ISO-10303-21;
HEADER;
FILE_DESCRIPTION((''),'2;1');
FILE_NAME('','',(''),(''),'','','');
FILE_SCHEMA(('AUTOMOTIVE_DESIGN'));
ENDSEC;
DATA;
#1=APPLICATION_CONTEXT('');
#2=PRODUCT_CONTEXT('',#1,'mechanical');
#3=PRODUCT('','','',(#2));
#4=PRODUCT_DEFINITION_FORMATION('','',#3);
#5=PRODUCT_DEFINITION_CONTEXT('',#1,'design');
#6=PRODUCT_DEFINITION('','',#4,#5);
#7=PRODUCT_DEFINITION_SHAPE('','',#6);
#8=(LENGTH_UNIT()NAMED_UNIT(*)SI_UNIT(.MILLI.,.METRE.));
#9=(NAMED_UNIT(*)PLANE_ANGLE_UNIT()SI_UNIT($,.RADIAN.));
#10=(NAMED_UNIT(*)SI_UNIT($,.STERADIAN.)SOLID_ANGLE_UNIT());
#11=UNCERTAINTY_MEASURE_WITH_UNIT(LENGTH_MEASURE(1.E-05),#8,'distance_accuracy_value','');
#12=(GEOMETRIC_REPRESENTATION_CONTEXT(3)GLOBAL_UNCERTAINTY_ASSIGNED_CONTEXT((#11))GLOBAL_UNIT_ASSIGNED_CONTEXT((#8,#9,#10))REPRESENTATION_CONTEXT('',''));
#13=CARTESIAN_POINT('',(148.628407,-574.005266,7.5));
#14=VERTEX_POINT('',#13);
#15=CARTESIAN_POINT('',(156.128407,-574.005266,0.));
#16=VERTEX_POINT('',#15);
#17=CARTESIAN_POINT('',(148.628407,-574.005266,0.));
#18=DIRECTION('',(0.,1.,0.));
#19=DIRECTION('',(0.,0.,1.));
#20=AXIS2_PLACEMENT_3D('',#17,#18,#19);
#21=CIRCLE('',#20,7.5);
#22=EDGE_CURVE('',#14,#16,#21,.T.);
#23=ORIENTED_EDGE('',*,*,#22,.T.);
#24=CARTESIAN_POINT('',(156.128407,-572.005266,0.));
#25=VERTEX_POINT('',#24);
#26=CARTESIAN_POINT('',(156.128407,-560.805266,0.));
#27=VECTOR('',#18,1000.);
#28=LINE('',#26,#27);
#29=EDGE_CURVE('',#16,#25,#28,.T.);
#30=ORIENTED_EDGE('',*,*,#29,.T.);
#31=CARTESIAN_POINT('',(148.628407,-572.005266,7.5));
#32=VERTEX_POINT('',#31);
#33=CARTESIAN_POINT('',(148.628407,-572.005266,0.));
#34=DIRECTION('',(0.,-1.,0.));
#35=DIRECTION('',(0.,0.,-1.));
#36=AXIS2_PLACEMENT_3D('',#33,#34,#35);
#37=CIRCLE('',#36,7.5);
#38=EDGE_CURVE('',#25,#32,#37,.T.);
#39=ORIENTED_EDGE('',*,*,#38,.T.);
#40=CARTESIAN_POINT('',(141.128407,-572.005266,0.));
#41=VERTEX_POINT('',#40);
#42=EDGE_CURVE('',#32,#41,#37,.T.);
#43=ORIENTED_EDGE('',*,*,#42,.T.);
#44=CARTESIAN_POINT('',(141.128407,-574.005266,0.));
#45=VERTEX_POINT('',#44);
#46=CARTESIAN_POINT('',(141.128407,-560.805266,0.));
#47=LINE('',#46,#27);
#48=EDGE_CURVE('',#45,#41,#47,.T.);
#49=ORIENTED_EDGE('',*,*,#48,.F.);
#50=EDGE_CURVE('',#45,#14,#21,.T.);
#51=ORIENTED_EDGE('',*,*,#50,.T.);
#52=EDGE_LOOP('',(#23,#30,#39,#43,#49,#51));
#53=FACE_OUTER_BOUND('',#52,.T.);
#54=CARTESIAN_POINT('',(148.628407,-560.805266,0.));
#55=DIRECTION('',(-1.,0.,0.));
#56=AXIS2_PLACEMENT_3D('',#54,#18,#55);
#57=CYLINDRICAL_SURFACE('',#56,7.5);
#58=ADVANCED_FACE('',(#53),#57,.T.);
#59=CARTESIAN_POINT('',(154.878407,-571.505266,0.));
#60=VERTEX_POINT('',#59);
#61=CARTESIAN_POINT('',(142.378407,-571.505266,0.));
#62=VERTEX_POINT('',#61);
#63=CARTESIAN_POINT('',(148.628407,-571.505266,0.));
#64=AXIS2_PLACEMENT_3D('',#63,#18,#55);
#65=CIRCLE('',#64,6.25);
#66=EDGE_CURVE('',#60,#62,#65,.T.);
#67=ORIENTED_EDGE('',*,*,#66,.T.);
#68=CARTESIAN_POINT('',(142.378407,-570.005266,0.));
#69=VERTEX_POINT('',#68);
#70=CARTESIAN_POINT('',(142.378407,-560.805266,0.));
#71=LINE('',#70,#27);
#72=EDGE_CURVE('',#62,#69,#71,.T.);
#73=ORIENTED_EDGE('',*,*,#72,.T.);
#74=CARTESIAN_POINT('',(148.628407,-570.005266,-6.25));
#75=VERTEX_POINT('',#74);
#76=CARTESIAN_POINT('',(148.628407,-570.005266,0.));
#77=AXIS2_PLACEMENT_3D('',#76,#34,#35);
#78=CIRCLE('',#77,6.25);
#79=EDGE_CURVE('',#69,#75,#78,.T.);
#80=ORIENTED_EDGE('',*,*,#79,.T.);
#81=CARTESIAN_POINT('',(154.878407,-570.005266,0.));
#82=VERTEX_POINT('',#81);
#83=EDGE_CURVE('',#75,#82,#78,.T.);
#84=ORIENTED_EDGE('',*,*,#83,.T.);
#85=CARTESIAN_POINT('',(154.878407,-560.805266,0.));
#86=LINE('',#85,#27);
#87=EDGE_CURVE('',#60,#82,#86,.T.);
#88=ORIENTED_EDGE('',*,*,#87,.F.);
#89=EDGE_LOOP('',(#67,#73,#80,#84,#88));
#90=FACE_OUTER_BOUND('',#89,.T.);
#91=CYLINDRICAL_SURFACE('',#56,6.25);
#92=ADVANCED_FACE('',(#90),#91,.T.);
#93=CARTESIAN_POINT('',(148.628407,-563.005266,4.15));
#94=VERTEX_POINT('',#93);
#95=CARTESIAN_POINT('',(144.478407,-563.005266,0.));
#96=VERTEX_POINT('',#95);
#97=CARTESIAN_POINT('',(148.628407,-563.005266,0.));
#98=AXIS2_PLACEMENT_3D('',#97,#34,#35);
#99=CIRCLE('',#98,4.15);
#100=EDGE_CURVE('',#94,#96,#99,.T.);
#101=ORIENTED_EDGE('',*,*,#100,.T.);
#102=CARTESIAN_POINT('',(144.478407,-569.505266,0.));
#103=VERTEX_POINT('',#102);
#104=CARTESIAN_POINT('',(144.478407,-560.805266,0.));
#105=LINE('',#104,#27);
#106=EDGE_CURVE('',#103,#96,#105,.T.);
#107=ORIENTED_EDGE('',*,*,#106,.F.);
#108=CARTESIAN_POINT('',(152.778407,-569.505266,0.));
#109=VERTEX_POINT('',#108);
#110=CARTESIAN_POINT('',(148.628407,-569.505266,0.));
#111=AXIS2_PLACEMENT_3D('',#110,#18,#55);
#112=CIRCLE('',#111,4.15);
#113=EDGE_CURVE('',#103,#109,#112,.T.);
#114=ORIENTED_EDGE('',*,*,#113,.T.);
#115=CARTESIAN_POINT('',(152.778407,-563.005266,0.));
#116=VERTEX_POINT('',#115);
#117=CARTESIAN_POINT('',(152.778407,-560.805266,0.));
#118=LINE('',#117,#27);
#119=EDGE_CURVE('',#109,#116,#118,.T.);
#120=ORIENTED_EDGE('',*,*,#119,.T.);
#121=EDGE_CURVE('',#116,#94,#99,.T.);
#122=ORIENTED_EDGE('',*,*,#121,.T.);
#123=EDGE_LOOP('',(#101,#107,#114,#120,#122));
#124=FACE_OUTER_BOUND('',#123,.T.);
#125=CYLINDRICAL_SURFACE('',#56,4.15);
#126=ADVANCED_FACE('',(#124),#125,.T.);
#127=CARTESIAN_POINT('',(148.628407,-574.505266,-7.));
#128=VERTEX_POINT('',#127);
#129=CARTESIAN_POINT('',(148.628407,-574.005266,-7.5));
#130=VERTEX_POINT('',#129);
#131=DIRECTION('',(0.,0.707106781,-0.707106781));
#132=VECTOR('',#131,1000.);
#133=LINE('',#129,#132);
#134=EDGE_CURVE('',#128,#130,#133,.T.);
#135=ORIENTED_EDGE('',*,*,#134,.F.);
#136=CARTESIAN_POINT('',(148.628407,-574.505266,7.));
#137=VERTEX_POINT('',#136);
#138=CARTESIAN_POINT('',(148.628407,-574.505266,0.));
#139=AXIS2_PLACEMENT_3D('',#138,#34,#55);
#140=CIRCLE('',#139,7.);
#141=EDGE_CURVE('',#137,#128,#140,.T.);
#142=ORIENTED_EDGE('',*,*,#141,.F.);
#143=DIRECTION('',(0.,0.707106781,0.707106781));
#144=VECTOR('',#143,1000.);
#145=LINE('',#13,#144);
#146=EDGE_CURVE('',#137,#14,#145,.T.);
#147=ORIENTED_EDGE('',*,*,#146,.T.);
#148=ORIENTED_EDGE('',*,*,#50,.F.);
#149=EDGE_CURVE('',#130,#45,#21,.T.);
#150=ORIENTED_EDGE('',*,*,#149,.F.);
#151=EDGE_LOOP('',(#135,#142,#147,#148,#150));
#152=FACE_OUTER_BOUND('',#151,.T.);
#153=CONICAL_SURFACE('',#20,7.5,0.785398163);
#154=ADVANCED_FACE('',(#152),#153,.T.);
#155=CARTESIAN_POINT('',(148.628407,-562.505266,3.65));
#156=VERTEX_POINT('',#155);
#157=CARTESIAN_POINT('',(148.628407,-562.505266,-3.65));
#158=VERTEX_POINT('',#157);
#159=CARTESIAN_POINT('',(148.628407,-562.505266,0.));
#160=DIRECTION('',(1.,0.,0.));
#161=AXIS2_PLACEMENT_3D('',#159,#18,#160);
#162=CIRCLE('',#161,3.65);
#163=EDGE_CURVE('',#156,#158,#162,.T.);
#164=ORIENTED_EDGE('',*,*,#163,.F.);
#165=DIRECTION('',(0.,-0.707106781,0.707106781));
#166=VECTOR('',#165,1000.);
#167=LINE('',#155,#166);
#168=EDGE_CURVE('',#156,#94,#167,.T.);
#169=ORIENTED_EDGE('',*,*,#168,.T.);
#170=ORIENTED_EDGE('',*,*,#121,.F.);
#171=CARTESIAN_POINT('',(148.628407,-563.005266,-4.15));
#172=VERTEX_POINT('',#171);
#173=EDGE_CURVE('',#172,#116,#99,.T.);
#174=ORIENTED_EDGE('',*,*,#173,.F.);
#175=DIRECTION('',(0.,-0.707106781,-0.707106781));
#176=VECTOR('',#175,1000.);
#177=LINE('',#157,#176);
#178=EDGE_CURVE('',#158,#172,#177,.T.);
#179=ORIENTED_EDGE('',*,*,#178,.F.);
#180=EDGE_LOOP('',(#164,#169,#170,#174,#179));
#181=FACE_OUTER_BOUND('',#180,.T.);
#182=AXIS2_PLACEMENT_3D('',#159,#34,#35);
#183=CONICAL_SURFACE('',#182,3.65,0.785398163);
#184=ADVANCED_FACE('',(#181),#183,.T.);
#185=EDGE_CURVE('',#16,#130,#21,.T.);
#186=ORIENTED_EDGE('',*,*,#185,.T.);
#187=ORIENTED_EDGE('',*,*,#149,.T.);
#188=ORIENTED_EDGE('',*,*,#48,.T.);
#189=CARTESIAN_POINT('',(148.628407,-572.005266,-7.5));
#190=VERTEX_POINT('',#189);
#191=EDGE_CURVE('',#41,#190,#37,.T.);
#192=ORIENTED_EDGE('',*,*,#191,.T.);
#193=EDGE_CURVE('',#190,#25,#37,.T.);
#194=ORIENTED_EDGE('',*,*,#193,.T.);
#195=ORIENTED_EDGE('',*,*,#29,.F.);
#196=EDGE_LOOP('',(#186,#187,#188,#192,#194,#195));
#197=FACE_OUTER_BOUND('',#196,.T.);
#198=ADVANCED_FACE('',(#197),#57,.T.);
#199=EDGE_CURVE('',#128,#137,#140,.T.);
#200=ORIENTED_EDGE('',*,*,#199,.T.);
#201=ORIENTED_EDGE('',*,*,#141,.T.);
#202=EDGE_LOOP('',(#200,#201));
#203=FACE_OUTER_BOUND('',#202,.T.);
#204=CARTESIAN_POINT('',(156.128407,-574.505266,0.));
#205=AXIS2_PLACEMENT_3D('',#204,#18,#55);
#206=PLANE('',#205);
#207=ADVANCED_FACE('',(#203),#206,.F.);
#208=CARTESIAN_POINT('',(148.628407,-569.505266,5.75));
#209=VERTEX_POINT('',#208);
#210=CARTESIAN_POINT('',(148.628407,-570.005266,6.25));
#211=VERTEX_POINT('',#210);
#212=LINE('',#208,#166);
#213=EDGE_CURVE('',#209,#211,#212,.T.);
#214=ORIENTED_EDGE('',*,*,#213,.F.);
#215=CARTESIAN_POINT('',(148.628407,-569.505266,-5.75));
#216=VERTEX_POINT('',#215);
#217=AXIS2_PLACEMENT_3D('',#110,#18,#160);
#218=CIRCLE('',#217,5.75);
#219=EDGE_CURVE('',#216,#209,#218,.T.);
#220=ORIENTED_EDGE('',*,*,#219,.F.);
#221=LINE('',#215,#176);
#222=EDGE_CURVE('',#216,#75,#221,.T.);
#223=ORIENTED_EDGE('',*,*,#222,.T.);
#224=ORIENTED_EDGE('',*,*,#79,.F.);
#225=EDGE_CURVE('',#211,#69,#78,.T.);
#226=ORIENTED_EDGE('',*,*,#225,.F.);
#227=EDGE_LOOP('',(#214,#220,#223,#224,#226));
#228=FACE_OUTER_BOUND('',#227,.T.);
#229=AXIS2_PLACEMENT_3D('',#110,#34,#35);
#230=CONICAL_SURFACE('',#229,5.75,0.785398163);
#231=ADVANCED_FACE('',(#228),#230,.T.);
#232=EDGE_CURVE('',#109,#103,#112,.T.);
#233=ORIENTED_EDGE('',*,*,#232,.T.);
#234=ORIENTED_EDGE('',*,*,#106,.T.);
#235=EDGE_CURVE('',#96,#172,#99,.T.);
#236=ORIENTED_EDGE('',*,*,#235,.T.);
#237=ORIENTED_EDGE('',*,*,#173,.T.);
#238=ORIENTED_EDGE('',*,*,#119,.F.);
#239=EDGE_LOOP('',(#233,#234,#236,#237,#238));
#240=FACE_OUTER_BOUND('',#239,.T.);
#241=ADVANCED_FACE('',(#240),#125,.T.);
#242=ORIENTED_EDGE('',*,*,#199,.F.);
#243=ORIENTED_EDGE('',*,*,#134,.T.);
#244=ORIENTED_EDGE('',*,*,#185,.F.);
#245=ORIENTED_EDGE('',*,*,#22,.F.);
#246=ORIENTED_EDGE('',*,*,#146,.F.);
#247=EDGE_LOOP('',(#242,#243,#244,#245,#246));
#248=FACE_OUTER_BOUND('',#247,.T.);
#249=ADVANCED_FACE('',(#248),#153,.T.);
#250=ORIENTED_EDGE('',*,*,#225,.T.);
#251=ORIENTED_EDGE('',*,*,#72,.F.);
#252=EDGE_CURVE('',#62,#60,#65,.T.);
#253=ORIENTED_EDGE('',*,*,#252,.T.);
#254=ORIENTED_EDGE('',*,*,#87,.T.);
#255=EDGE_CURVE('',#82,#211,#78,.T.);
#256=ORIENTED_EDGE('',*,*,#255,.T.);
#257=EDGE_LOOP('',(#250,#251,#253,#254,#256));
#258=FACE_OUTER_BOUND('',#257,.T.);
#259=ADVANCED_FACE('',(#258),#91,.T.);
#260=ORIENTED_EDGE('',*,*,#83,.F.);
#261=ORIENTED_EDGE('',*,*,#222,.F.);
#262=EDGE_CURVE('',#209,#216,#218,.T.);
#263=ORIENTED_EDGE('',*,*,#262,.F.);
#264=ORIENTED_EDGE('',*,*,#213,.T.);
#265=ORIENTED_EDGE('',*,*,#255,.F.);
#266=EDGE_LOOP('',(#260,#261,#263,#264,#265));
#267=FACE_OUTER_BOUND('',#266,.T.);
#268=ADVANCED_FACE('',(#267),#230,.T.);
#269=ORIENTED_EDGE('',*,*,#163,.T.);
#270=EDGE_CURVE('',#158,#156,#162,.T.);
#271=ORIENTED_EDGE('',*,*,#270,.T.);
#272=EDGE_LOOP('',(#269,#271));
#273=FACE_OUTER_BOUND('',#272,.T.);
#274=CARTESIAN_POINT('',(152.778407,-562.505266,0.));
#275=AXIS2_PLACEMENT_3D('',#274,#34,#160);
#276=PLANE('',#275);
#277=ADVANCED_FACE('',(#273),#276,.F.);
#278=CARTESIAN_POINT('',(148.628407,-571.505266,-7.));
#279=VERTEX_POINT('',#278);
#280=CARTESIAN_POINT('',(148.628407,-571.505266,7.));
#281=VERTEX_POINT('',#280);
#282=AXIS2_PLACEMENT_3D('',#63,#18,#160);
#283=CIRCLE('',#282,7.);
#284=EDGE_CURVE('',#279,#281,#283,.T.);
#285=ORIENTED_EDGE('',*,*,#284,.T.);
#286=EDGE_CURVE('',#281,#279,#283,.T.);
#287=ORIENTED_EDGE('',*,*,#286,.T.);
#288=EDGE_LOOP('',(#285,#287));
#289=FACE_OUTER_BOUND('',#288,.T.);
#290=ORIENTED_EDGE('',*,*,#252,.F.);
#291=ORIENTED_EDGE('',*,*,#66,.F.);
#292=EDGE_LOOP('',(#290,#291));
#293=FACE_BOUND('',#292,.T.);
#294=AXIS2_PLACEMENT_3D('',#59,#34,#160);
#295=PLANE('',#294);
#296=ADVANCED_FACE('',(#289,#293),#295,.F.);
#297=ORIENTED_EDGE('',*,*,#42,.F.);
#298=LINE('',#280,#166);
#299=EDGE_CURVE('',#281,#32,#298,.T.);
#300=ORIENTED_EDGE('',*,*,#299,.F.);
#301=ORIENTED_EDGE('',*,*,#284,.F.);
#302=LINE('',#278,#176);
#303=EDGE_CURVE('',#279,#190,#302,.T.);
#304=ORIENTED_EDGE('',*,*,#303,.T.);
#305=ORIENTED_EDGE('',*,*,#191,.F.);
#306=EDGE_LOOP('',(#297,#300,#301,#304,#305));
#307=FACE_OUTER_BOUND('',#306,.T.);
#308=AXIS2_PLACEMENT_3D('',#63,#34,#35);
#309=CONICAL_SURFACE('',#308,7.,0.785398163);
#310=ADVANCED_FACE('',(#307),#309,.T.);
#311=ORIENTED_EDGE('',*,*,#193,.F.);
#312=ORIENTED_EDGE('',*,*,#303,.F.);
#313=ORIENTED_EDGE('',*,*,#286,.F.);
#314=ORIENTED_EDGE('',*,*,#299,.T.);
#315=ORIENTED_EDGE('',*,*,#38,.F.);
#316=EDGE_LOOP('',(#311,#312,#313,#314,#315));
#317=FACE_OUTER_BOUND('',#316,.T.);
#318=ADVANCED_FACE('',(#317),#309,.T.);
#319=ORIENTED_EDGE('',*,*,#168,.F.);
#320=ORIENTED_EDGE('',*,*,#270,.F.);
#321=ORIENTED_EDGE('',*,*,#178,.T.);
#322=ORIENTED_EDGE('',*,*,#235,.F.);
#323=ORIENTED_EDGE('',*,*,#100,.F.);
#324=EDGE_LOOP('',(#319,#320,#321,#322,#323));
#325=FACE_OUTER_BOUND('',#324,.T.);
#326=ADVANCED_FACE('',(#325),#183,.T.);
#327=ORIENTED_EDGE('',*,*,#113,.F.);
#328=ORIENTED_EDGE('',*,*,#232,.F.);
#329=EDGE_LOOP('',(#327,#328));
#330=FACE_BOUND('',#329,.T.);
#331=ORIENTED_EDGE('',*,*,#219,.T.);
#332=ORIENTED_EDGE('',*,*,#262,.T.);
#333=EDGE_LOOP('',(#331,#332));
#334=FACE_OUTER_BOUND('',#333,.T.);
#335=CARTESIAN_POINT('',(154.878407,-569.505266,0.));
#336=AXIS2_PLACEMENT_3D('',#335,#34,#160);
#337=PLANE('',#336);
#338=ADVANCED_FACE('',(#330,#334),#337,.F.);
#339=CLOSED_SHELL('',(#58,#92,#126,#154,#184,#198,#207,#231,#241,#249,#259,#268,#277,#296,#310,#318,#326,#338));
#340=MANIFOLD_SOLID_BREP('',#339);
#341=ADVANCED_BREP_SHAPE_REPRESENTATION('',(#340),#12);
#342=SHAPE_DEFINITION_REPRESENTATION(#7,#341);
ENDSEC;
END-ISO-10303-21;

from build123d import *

# Parameters (mm, degrees)
CHAMFER1_SIZE = 0.5


with BuildPart() as part:
    # Sketch1 → Revolve1 (revolve)
    with BuildSketch(Plane.XY, mode=Mode.PRIVATE) as revolve1_sk:
        Polygon((154.87840727, -569.505265962), (152.77840727, -569.505265962), (152.77840727, -562.505265962), (148.62840727, -562.505265962), (148.62840727, -574.505265962), (156.12840727, -574.505265962), (156.12840727, -571.505265962), (154.87840727, -571.505265962), align=None)
    revolve(revolve1_sk.sketch.rotate(Axis((148.62840727, -560.805265962, 0), (0, -1, 0)), 180), axis=Axis((148.62840727, -560.805265962, 0), (0, -1, 0)))

    # Chamfer1
    chamfer1_edges = [part.edges().sort_by_distance(p)[0] for p in [
        (154.87840727, -569.505265962, 0),
        (156.12840727, -571.505265962, 0),
        (156.12840727, -574.505265962, 0),
        (152.77840727, -562.505265962, 0),
    ]]
    chamfer(chamfer1_edges, length=CHAMFER1_SIZE)


solid = part.part
